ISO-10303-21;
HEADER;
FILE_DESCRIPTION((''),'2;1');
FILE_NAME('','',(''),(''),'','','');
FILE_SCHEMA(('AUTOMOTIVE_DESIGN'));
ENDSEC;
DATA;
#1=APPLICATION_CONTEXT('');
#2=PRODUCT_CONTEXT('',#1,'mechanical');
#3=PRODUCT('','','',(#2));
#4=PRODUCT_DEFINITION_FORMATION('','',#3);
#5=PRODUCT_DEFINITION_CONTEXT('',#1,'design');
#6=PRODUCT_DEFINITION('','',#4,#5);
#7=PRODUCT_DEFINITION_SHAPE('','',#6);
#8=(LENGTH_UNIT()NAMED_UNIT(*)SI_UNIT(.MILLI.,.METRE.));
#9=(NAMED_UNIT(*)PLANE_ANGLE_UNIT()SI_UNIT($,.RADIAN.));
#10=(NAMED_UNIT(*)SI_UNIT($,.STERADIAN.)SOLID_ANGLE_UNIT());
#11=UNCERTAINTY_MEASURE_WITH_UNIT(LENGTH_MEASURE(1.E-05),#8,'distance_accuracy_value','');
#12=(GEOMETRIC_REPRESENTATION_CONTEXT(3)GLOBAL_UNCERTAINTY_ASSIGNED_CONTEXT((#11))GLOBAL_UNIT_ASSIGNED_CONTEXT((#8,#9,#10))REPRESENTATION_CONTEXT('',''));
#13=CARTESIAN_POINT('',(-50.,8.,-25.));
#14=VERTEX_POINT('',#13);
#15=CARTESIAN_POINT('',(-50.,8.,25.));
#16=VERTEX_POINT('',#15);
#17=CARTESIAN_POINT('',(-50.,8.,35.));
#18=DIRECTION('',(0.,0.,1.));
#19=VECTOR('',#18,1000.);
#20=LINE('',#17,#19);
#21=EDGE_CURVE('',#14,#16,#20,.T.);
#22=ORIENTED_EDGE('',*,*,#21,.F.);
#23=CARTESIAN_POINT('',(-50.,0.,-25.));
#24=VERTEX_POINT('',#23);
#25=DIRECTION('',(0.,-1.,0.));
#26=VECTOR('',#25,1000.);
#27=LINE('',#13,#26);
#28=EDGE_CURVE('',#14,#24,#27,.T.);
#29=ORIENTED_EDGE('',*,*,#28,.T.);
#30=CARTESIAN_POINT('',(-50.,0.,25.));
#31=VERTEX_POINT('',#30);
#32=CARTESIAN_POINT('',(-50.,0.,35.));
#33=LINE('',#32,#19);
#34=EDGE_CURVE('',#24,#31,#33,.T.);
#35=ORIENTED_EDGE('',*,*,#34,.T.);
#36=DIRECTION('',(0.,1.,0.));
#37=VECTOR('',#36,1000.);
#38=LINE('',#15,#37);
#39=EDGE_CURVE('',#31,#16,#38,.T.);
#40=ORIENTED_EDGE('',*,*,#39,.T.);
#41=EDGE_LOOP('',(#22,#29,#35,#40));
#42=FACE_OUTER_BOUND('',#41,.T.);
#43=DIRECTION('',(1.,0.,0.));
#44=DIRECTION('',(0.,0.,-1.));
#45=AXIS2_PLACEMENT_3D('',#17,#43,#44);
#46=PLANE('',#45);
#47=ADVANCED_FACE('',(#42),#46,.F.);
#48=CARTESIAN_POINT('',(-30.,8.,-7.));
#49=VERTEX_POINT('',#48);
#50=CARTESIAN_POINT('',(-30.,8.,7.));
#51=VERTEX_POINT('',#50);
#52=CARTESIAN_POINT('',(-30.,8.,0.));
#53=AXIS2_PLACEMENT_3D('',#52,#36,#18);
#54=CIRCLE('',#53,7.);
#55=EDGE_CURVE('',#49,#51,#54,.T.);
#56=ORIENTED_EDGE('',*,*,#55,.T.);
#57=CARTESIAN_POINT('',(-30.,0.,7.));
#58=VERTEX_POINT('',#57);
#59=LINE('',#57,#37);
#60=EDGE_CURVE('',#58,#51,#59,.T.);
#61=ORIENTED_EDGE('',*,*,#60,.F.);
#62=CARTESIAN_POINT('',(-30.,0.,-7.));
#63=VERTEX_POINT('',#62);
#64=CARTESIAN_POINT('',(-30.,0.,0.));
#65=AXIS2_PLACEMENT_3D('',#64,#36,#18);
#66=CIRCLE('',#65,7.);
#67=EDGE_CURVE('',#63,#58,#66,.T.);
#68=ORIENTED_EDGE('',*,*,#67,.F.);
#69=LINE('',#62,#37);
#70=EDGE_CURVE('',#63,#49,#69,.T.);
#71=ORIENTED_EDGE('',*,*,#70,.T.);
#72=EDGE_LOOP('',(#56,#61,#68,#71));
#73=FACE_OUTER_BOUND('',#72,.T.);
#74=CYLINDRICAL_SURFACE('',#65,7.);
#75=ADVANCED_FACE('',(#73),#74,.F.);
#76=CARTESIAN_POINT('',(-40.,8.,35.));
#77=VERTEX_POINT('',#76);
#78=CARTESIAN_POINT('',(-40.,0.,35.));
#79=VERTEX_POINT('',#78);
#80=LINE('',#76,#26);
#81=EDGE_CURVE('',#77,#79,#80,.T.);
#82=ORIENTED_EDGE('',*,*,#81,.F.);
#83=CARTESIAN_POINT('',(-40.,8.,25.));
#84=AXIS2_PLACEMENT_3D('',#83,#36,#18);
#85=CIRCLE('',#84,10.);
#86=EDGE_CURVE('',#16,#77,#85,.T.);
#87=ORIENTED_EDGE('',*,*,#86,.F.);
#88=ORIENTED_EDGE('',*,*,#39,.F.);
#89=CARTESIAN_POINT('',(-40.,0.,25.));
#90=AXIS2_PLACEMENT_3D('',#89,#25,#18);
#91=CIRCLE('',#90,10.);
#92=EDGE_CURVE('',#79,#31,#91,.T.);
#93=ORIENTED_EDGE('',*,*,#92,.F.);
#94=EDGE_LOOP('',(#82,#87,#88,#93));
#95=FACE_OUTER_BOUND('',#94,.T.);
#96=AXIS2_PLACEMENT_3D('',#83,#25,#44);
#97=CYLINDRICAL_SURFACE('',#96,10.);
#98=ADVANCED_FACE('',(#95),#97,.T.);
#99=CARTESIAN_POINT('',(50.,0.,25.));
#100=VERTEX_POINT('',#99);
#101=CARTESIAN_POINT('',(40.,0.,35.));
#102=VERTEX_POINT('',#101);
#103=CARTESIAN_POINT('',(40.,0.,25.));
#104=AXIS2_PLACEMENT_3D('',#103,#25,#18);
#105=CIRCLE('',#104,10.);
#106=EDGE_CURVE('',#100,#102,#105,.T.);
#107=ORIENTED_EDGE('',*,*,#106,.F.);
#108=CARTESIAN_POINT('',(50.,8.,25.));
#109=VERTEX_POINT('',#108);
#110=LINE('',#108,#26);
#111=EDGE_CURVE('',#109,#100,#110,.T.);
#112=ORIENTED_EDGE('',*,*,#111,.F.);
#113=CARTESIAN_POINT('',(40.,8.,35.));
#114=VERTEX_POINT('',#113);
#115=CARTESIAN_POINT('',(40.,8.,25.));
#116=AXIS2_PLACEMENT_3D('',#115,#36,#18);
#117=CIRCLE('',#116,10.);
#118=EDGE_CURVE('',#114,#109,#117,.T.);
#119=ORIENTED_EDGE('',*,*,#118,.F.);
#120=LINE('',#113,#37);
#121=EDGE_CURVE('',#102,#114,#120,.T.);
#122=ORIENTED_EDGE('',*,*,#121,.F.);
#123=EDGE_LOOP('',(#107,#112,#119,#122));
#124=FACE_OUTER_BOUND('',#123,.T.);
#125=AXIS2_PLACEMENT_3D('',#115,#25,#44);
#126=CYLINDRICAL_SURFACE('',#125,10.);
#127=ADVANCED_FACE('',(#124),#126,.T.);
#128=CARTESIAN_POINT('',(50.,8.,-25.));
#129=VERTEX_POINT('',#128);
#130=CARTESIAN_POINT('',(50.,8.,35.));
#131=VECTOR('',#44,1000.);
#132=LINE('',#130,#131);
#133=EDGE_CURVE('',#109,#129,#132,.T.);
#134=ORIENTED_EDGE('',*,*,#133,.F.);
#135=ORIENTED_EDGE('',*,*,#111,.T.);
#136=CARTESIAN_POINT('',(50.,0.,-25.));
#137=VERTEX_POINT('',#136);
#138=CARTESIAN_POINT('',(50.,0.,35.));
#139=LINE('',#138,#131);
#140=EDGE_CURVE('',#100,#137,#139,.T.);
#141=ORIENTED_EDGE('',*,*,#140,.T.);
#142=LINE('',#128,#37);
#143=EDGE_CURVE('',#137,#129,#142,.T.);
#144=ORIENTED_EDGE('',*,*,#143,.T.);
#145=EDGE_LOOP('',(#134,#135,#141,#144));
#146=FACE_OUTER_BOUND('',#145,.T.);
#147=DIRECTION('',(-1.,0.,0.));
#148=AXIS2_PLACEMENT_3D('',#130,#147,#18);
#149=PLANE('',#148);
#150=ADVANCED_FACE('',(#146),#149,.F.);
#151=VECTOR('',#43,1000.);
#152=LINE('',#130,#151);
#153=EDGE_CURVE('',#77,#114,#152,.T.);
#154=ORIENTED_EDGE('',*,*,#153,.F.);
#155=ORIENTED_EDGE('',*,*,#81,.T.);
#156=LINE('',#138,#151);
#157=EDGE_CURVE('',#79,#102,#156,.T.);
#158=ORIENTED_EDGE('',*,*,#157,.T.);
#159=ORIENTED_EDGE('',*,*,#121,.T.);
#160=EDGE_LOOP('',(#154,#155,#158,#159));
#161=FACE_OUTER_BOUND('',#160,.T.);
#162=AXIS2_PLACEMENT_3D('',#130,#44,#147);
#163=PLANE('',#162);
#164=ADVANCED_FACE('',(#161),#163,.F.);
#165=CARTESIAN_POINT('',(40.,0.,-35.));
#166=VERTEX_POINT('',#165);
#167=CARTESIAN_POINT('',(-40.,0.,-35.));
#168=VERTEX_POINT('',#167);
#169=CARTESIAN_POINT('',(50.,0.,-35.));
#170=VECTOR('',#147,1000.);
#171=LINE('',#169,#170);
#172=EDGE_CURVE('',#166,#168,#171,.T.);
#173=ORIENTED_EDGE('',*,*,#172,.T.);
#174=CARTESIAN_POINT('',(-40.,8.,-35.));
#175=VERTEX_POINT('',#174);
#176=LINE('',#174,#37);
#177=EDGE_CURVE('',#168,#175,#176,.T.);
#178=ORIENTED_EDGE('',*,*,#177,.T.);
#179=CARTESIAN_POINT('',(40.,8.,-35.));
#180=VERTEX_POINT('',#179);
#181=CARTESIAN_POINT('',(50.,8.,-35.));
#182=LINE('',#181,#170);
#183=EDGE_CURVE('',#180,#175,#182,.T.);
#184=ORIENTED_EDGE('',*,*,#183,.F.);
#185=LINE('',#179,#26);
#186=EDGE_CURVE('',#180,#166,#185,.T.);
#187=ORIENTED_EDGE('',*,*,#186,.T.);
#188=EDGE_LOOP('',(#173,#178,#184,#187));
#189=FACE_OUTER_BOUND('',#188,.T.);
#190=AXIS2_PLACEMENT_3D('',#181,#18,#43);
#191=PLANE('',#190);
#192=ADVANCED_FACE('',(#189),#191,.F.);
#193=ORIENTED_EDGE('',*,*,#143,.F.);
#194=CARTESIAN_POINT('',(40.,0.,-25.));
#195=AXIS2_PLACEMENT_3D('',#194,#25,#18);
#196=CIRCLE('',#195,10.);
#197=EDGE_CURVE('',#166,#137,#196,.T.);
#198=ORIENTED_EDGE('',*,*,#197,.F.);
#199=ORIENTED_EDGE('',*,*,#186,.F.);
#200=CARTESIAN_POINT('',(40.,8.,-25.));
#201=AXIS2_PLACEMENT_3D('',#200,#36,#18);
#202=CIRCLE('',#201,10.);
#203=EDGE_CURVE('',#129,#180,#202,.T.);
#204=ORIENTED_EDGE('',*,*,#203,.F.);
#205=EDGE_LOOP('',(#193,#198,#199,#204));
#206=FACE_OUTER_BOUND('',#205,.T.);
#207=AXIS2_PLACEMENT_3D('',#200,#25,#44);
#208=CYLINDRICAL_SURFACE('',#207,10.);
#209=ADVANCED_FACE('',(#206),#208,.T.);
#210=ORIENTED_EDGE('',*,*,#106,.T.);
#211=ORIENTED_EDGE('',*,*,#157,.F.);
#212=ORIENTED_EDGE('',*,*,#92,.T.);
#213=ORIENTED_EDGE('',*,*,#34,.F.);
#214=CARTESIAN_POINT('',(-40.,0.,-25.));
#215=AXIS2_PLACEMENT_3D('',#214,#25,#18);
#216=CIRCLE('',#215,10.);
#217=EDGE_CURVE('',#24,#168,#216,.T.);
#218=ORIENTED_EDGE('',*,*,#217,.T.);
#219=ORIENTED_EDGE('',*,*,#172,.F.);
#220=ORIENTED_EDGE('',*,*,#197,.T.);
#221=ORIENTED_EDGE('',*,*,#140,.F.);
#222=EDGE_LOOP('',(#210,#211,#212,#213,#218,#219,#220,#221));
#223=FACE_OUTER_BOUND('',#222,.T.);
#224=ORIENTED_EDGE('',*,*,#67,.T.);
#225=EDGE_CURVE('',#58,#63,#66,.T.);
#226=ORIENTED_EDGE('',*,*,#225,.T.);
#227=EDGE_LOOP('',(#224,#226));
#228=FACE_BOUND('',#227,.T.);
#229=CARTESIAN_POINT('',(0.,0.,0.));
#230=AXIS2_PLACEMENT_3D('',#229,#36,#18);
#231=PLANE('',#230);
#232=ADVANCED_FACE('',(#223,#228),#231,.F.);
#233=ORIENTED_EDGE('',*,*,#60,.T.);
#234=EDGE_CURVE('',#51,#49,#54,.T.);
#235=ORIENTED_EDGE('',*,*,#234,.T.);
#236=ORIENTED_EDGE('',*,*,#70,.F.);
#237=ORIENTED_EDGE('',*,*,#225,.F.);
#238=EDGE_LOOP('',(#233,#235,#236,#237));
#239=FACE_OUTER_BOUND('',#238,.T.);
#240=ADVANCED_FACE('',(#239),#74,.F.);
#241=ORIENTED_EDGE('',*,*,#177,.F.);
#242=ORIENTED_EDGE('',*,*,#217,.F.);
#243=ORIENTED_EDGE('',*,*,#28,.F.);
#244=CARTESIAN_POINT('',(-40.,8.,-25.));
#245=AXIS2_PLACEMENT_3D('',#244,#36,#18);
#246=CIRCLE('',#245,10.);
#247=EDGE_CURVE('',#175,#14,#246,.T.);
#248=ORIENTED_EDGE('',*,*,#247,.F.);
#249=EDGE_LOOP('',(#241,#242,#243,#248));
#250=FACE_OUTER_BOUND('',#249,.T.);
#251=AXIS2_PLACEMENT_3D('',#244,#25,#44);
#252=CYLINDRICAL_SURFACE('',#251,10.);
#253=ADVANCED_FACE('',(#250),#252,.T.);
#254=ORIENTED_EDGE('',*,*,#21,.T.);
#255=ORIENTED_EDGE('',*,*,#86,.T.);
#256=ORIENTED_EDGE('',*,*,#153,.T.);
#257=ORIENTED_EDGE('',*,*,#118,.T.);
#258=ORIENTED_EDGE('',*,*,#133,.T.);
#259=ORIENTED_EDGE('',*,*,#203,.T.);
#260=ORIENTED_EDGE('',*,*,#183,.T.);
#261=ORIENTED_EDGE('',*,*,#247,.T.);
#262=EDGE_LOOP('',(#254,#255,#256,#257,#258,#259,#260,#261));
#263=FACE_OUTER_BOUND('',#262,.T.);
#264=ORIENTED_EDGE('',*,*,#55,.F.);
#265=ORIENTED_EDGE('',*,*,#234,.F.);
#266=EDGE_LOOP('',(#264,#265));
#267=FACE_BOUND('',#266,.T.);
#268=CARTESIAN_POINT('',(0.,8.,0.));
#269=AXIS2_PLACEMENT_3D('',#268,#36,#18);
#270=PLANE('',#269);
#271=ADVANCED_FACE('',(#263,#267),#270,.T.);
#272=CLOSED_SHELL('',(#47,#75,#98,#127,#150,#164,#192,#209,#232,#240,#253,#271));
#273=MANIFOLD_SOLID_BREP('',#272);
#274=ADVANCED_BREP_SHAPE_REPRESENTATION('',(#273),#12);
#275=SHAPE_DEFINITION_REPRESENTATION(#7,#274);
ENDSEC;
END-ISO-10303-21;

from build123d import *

# Parameters (mm, degrees)
SKETCH1_W           = 100
SKETCH1_H           = 70
BOSS_EXTRUDE1_DEPTH = 8
FILLET1_R           = 10
SKETCH2_R           = 7
CUT_EXTRUDE1_DEPTH  = 8


with BuildPart() as part:
    # Sketch1 → Boss-Extrude1 (new body)
    with BuildSketch(Plane(origin=(0, 0, 0), x_dir=(1, 0, 0), z_dir=(0, 1, 0))):
        Rectangle(SKETCH1_W, SKETCH1_H)
    extrude(amount=BOSS_EXTRUDE1_DEPTH)

    # Fillet1
    fillet1_edges = [part.edges().sort_by_distance(p)[0] for p in [
        (-50, 4, -35),
        (50, 4, -35),
        (50, 4, 35),
        (-50, 4, 35),
    ]]
    fillet(fillet1_edges, radius=FILLET1_R)

    # Sketch2 → Cut-Extrude1 (cut)
    with BuildSketch(Plane(origin=(0, 8, 0), x_dir=(1, 0, 0), z_dir=(0, 1, 0))):
        with Locations(Location((-30, 0, 0), (0, 0, 270))):
            Circle(SKETCH2_R)
    extrude(amount=-CUT_EXTRUDE1_DEPTH, mode=Mode.SUBTRACT)


solid = part.part
